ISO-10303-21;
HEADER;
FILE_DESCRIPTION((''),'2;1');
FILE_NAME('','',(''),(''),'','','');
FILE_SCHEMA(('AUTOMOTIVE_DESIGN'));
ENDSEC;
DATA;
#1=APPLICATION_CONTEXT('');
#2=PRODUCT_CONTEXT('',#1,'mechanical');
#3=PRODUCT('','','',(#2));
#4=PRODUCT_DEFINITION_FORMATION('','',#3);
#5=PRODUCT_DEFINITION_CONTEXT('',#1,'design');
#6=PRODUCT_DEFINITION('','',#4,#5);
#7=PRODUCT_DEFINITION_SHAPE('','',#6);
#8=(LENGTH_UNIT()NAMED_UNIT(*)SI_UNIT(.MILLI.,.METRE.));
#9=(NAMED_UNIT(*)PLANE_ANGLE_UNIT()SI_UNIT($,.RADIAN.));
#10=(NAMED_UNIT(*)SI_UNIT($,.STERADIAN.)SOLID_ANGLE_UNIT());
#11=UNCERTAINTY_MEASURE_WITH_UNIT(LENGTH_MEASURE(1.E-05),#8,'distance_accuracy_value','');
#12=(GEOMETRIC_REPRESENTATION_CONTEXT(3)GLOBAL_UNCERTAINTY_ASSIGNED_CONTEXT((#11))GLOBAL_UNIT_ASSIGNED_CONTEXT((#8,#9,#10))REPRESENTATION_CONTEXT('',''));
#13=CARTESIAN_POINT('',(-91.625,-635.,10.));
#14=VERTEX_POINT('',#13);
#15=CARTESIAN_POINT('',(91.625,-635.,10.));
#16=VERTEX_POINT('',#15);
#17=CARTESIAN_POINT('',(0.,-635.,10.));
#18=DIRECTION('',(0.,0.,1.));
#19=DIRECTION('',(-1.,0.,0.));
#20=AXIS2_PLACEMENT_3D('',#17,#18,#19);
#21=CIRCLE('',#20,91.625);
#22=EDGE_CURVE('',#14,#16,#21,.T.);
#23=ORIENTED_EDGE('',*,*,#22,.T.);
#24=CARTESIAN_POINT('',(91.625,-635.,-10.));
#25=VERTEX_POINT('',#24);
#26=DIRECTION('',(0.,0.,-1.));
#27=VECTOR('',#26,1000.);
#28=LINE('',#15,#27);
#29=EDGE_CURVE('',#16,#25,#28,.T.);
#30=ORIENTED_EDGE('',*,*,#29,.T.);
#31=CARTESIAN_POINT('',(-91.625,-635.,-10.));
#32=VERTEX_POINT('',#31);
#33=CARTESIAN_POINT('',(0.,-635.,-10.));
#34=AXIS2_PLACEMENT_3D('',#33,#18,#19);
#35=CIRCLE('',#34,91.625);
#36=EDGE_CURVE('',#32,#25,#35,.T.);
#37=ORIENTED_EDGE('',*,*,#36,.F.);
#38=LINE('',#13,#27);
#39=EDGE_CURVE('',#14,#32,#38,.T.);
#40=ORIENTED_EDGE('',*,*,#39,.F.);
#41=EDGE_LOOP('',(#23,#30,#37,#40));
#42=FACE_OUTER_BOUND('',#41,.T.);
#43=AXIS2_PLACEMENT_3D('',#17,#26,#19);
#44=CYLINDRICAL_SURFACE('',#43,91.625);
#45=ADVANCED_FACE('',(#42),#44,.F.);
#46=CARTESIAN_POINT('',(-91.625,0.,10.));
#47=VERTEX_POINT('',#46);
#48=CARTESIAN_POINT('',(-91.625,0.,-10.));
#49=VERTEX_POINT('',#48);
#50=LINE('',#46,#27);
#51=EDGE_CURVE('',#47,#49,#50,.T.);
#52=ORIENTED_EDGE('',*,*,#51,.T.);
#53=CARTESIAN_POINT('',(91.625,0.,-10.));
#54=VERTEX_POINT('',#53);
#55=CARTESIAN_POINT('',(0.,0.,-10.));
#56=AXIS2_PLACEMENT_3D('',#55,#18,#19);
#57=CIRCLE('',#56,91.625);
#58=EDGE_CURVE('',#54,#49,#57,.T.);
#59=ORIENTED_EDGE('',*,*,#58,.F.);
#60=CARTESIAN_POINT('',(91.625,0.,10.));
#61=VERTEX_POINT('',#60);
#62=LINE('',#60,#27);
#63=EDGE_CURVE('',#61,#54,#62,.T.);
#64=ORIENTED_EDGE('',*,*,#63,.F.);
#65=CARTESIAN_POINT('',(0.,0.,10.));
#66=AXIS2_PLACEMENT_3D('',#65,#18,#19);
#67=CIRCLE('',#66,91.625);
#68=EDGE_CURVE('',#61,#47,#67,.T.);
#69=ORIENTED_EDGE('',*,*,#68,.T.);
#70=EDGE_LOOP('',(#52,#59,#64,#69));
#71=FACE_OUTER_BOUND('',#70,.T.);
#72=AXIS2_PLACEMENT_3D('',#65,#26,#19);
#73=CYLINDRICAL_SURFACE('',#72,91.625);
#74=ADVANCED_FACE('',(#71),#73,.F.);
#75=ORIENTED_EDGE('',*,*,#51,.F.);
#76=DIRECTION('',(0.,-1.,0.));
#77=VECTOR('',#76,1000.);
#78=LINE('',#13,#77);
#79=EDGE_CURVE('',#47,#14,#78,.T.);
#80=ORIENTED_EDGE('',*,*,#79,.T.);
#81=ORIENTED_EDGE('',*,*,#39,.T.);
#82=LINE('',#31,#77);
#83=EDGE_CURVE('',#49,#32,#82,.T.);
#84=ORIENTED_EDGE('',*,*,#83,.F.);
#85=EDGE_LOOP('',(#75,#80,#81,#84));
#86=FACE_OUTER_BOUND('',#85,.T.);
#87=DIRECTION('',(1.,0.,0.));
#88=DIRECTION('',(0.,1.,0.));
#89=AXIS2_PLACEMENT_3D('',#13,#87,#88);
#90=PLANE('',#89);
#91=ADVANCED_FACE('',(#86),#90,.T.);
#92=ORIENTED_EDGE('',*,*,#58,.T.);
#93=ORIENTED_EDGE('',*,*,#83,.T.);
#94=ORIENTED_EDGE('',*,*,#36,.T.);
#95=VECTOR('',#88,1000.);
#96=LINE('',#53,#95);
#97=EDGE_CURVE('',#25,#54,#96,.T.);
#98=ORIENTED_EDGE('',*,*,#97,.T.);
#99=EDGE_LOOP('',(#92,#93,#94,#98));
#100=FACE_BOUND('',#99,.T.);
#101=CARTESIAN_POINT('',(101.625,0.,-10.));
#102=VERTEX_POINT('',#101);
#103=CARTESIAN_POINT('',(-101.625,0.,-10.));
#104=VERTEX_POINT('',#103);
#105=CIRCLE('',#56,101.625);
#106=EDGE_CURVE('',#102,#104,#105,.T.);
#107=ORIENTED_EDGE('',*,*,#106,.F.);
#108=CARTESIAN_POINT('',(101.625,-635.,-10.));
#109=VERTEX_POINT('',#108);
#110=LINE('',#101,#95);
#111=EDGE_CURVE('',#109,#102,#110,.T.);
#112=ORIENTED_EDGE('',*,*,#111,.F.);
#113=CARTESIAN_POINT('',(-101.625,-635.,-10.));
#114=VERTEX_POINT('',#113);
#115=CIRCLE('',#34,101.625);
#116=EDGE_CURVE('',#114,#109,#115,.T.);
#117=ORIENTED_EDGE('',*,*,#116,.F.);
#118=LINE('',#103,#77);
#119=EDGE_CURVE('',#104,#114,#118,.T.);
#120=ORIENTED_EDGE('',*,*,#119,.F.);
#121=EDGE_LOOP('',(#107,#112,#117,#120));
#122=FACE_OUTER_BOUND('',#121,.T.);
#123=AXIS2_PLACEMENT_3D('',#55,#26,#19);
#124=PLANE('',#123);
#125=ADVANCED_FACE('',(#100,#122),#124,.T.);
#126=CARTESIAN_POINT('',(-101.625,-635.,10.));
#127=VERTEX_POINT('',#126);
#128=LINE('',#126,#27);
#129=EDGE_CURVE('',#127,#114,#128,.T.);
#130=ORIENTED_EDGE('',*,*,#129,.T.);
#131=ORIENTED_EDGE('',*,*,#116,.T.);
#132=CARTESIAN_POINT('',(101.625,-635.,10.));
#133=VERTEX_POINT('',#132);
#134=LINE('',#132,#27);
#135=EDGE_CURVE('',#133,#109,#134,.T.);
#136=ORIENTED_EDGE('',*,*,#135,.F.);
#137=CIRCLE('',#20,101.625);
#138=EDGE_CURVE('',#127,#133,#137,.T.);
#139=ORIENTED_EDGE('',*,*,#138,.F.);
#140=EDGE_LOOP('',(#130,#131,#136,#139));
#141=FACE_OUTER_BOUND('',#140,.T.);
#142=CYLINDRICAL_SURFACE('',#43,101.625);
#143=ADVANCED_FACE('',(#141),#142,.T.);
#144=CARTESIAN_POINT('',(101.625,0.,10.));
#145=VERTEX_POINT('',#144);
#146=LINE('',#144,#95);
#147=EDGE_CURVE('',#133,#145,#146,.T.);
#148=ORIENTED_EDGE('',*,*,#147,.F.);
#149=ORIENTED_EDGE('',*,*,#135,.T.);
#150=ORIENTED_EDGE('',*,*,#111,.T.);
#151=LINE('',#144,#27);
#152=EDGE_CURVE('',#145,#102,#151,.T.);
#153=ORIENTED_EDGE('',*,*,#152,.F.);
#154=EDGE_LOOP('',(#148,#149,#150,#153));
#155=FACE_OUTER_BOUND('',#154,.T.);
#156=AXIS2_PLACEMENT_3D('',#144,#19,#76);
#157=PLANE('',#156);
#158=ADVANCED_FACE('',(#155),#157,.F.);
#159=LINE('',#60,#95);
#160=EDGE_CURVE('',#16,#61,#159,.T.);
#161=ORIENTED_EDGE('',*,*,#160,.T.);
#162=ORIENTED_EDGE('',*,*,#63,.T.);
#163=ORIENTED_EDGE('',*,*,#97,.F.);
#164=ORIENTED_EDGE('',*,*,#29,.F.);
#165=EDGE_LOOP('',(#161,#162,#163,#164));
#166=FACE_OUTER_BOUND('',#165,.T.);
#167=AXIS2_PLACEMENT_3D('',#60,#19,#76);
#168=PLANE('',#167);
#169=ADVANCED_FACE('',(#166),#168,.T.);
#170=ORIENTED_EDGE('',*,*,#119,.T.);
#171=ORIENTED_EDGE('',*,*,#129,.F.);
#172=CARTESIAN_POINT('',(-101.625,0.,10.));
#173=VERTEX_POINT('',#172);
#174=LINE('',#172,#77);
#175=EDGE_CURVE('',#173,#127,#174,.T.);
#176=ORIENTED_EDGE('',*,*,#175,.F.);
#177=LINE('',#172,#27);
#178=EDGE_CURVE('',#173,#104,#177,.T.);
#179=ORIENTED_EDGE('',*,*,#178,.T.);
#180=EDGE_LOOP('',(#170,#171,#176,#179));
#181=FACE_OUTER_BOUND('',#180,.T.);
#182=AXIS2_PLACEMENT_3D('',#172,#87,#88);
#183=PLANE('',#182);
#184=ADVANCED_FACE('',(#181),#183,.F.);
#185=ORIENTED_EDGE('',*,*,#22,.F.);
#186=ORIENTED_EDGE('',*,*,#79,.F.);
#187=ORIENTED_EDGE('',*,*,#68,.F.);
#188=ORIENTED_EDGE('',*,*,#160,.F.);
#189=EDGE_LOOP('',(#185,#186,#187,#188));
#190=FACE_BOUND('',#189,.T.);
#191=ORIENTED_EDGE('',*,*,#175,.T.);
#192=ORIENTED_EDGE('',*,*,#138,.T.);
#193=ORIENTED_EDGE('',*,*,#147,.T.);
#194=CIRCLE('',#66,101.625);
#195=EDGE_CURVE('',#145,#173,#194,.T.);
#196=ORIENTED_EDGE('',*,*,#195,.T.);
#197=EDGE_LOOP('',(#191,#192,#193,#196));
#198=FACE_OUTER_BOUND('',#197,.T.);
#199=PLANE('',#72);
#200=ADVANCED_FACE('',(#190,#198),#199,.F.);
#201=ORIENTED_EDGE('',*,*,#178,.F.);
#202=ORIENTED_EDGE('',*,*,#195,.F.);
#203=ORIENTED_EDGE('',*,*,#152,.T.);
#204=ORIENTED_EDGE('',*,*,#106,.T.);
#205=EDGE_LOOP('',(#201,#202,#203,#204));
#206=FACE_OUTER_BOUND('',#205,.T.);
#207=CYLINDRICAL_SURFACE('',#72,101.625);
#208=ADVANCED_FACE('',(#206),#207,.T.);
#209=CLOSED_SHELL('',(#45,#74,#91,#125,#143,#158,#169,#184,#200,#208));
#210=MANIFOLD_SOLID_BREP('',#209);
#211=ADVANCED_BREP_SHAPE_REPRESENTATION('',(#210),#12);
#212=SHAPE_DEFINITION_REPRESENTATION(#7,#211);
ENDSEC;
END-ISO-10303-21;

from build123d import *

# Parameters (mm, degrees)
EXTRUDE_1_DEPTH = 10


with BuildPart() as part:
    # 草图2 → 拉伸-薄壁1 (new, symmetric)
    with BuildSketch(Plane.XY):
        with BuildLine():
            Line((-101.625, -635), (-101.625, 0))
            ThreePointArc((-101.625, 0), (0, 101.625), (101.625, 0))
            Line((101.625, 0), (101.625, -635))
            ThreePointArc((101.625, -635), (0, -736.625), (-101.625, -635))
        make_face()
        with BuildLine():
            Line((-91.625, -635), (-91.625, 0))
            ThreePointArc((-91.625, 0), (0, 91.625), (91.625, 0))
            Line((91.625, 0), (91.625, -635))
            ThreePointArc((91.625, -635), (0, -726.625), (-91.625, -635))
        make_face(mode=Mode.SUBTRACT)
    extrude(amount=EXTRUDE_1_DEPTH, both=True)


solid = part.part
